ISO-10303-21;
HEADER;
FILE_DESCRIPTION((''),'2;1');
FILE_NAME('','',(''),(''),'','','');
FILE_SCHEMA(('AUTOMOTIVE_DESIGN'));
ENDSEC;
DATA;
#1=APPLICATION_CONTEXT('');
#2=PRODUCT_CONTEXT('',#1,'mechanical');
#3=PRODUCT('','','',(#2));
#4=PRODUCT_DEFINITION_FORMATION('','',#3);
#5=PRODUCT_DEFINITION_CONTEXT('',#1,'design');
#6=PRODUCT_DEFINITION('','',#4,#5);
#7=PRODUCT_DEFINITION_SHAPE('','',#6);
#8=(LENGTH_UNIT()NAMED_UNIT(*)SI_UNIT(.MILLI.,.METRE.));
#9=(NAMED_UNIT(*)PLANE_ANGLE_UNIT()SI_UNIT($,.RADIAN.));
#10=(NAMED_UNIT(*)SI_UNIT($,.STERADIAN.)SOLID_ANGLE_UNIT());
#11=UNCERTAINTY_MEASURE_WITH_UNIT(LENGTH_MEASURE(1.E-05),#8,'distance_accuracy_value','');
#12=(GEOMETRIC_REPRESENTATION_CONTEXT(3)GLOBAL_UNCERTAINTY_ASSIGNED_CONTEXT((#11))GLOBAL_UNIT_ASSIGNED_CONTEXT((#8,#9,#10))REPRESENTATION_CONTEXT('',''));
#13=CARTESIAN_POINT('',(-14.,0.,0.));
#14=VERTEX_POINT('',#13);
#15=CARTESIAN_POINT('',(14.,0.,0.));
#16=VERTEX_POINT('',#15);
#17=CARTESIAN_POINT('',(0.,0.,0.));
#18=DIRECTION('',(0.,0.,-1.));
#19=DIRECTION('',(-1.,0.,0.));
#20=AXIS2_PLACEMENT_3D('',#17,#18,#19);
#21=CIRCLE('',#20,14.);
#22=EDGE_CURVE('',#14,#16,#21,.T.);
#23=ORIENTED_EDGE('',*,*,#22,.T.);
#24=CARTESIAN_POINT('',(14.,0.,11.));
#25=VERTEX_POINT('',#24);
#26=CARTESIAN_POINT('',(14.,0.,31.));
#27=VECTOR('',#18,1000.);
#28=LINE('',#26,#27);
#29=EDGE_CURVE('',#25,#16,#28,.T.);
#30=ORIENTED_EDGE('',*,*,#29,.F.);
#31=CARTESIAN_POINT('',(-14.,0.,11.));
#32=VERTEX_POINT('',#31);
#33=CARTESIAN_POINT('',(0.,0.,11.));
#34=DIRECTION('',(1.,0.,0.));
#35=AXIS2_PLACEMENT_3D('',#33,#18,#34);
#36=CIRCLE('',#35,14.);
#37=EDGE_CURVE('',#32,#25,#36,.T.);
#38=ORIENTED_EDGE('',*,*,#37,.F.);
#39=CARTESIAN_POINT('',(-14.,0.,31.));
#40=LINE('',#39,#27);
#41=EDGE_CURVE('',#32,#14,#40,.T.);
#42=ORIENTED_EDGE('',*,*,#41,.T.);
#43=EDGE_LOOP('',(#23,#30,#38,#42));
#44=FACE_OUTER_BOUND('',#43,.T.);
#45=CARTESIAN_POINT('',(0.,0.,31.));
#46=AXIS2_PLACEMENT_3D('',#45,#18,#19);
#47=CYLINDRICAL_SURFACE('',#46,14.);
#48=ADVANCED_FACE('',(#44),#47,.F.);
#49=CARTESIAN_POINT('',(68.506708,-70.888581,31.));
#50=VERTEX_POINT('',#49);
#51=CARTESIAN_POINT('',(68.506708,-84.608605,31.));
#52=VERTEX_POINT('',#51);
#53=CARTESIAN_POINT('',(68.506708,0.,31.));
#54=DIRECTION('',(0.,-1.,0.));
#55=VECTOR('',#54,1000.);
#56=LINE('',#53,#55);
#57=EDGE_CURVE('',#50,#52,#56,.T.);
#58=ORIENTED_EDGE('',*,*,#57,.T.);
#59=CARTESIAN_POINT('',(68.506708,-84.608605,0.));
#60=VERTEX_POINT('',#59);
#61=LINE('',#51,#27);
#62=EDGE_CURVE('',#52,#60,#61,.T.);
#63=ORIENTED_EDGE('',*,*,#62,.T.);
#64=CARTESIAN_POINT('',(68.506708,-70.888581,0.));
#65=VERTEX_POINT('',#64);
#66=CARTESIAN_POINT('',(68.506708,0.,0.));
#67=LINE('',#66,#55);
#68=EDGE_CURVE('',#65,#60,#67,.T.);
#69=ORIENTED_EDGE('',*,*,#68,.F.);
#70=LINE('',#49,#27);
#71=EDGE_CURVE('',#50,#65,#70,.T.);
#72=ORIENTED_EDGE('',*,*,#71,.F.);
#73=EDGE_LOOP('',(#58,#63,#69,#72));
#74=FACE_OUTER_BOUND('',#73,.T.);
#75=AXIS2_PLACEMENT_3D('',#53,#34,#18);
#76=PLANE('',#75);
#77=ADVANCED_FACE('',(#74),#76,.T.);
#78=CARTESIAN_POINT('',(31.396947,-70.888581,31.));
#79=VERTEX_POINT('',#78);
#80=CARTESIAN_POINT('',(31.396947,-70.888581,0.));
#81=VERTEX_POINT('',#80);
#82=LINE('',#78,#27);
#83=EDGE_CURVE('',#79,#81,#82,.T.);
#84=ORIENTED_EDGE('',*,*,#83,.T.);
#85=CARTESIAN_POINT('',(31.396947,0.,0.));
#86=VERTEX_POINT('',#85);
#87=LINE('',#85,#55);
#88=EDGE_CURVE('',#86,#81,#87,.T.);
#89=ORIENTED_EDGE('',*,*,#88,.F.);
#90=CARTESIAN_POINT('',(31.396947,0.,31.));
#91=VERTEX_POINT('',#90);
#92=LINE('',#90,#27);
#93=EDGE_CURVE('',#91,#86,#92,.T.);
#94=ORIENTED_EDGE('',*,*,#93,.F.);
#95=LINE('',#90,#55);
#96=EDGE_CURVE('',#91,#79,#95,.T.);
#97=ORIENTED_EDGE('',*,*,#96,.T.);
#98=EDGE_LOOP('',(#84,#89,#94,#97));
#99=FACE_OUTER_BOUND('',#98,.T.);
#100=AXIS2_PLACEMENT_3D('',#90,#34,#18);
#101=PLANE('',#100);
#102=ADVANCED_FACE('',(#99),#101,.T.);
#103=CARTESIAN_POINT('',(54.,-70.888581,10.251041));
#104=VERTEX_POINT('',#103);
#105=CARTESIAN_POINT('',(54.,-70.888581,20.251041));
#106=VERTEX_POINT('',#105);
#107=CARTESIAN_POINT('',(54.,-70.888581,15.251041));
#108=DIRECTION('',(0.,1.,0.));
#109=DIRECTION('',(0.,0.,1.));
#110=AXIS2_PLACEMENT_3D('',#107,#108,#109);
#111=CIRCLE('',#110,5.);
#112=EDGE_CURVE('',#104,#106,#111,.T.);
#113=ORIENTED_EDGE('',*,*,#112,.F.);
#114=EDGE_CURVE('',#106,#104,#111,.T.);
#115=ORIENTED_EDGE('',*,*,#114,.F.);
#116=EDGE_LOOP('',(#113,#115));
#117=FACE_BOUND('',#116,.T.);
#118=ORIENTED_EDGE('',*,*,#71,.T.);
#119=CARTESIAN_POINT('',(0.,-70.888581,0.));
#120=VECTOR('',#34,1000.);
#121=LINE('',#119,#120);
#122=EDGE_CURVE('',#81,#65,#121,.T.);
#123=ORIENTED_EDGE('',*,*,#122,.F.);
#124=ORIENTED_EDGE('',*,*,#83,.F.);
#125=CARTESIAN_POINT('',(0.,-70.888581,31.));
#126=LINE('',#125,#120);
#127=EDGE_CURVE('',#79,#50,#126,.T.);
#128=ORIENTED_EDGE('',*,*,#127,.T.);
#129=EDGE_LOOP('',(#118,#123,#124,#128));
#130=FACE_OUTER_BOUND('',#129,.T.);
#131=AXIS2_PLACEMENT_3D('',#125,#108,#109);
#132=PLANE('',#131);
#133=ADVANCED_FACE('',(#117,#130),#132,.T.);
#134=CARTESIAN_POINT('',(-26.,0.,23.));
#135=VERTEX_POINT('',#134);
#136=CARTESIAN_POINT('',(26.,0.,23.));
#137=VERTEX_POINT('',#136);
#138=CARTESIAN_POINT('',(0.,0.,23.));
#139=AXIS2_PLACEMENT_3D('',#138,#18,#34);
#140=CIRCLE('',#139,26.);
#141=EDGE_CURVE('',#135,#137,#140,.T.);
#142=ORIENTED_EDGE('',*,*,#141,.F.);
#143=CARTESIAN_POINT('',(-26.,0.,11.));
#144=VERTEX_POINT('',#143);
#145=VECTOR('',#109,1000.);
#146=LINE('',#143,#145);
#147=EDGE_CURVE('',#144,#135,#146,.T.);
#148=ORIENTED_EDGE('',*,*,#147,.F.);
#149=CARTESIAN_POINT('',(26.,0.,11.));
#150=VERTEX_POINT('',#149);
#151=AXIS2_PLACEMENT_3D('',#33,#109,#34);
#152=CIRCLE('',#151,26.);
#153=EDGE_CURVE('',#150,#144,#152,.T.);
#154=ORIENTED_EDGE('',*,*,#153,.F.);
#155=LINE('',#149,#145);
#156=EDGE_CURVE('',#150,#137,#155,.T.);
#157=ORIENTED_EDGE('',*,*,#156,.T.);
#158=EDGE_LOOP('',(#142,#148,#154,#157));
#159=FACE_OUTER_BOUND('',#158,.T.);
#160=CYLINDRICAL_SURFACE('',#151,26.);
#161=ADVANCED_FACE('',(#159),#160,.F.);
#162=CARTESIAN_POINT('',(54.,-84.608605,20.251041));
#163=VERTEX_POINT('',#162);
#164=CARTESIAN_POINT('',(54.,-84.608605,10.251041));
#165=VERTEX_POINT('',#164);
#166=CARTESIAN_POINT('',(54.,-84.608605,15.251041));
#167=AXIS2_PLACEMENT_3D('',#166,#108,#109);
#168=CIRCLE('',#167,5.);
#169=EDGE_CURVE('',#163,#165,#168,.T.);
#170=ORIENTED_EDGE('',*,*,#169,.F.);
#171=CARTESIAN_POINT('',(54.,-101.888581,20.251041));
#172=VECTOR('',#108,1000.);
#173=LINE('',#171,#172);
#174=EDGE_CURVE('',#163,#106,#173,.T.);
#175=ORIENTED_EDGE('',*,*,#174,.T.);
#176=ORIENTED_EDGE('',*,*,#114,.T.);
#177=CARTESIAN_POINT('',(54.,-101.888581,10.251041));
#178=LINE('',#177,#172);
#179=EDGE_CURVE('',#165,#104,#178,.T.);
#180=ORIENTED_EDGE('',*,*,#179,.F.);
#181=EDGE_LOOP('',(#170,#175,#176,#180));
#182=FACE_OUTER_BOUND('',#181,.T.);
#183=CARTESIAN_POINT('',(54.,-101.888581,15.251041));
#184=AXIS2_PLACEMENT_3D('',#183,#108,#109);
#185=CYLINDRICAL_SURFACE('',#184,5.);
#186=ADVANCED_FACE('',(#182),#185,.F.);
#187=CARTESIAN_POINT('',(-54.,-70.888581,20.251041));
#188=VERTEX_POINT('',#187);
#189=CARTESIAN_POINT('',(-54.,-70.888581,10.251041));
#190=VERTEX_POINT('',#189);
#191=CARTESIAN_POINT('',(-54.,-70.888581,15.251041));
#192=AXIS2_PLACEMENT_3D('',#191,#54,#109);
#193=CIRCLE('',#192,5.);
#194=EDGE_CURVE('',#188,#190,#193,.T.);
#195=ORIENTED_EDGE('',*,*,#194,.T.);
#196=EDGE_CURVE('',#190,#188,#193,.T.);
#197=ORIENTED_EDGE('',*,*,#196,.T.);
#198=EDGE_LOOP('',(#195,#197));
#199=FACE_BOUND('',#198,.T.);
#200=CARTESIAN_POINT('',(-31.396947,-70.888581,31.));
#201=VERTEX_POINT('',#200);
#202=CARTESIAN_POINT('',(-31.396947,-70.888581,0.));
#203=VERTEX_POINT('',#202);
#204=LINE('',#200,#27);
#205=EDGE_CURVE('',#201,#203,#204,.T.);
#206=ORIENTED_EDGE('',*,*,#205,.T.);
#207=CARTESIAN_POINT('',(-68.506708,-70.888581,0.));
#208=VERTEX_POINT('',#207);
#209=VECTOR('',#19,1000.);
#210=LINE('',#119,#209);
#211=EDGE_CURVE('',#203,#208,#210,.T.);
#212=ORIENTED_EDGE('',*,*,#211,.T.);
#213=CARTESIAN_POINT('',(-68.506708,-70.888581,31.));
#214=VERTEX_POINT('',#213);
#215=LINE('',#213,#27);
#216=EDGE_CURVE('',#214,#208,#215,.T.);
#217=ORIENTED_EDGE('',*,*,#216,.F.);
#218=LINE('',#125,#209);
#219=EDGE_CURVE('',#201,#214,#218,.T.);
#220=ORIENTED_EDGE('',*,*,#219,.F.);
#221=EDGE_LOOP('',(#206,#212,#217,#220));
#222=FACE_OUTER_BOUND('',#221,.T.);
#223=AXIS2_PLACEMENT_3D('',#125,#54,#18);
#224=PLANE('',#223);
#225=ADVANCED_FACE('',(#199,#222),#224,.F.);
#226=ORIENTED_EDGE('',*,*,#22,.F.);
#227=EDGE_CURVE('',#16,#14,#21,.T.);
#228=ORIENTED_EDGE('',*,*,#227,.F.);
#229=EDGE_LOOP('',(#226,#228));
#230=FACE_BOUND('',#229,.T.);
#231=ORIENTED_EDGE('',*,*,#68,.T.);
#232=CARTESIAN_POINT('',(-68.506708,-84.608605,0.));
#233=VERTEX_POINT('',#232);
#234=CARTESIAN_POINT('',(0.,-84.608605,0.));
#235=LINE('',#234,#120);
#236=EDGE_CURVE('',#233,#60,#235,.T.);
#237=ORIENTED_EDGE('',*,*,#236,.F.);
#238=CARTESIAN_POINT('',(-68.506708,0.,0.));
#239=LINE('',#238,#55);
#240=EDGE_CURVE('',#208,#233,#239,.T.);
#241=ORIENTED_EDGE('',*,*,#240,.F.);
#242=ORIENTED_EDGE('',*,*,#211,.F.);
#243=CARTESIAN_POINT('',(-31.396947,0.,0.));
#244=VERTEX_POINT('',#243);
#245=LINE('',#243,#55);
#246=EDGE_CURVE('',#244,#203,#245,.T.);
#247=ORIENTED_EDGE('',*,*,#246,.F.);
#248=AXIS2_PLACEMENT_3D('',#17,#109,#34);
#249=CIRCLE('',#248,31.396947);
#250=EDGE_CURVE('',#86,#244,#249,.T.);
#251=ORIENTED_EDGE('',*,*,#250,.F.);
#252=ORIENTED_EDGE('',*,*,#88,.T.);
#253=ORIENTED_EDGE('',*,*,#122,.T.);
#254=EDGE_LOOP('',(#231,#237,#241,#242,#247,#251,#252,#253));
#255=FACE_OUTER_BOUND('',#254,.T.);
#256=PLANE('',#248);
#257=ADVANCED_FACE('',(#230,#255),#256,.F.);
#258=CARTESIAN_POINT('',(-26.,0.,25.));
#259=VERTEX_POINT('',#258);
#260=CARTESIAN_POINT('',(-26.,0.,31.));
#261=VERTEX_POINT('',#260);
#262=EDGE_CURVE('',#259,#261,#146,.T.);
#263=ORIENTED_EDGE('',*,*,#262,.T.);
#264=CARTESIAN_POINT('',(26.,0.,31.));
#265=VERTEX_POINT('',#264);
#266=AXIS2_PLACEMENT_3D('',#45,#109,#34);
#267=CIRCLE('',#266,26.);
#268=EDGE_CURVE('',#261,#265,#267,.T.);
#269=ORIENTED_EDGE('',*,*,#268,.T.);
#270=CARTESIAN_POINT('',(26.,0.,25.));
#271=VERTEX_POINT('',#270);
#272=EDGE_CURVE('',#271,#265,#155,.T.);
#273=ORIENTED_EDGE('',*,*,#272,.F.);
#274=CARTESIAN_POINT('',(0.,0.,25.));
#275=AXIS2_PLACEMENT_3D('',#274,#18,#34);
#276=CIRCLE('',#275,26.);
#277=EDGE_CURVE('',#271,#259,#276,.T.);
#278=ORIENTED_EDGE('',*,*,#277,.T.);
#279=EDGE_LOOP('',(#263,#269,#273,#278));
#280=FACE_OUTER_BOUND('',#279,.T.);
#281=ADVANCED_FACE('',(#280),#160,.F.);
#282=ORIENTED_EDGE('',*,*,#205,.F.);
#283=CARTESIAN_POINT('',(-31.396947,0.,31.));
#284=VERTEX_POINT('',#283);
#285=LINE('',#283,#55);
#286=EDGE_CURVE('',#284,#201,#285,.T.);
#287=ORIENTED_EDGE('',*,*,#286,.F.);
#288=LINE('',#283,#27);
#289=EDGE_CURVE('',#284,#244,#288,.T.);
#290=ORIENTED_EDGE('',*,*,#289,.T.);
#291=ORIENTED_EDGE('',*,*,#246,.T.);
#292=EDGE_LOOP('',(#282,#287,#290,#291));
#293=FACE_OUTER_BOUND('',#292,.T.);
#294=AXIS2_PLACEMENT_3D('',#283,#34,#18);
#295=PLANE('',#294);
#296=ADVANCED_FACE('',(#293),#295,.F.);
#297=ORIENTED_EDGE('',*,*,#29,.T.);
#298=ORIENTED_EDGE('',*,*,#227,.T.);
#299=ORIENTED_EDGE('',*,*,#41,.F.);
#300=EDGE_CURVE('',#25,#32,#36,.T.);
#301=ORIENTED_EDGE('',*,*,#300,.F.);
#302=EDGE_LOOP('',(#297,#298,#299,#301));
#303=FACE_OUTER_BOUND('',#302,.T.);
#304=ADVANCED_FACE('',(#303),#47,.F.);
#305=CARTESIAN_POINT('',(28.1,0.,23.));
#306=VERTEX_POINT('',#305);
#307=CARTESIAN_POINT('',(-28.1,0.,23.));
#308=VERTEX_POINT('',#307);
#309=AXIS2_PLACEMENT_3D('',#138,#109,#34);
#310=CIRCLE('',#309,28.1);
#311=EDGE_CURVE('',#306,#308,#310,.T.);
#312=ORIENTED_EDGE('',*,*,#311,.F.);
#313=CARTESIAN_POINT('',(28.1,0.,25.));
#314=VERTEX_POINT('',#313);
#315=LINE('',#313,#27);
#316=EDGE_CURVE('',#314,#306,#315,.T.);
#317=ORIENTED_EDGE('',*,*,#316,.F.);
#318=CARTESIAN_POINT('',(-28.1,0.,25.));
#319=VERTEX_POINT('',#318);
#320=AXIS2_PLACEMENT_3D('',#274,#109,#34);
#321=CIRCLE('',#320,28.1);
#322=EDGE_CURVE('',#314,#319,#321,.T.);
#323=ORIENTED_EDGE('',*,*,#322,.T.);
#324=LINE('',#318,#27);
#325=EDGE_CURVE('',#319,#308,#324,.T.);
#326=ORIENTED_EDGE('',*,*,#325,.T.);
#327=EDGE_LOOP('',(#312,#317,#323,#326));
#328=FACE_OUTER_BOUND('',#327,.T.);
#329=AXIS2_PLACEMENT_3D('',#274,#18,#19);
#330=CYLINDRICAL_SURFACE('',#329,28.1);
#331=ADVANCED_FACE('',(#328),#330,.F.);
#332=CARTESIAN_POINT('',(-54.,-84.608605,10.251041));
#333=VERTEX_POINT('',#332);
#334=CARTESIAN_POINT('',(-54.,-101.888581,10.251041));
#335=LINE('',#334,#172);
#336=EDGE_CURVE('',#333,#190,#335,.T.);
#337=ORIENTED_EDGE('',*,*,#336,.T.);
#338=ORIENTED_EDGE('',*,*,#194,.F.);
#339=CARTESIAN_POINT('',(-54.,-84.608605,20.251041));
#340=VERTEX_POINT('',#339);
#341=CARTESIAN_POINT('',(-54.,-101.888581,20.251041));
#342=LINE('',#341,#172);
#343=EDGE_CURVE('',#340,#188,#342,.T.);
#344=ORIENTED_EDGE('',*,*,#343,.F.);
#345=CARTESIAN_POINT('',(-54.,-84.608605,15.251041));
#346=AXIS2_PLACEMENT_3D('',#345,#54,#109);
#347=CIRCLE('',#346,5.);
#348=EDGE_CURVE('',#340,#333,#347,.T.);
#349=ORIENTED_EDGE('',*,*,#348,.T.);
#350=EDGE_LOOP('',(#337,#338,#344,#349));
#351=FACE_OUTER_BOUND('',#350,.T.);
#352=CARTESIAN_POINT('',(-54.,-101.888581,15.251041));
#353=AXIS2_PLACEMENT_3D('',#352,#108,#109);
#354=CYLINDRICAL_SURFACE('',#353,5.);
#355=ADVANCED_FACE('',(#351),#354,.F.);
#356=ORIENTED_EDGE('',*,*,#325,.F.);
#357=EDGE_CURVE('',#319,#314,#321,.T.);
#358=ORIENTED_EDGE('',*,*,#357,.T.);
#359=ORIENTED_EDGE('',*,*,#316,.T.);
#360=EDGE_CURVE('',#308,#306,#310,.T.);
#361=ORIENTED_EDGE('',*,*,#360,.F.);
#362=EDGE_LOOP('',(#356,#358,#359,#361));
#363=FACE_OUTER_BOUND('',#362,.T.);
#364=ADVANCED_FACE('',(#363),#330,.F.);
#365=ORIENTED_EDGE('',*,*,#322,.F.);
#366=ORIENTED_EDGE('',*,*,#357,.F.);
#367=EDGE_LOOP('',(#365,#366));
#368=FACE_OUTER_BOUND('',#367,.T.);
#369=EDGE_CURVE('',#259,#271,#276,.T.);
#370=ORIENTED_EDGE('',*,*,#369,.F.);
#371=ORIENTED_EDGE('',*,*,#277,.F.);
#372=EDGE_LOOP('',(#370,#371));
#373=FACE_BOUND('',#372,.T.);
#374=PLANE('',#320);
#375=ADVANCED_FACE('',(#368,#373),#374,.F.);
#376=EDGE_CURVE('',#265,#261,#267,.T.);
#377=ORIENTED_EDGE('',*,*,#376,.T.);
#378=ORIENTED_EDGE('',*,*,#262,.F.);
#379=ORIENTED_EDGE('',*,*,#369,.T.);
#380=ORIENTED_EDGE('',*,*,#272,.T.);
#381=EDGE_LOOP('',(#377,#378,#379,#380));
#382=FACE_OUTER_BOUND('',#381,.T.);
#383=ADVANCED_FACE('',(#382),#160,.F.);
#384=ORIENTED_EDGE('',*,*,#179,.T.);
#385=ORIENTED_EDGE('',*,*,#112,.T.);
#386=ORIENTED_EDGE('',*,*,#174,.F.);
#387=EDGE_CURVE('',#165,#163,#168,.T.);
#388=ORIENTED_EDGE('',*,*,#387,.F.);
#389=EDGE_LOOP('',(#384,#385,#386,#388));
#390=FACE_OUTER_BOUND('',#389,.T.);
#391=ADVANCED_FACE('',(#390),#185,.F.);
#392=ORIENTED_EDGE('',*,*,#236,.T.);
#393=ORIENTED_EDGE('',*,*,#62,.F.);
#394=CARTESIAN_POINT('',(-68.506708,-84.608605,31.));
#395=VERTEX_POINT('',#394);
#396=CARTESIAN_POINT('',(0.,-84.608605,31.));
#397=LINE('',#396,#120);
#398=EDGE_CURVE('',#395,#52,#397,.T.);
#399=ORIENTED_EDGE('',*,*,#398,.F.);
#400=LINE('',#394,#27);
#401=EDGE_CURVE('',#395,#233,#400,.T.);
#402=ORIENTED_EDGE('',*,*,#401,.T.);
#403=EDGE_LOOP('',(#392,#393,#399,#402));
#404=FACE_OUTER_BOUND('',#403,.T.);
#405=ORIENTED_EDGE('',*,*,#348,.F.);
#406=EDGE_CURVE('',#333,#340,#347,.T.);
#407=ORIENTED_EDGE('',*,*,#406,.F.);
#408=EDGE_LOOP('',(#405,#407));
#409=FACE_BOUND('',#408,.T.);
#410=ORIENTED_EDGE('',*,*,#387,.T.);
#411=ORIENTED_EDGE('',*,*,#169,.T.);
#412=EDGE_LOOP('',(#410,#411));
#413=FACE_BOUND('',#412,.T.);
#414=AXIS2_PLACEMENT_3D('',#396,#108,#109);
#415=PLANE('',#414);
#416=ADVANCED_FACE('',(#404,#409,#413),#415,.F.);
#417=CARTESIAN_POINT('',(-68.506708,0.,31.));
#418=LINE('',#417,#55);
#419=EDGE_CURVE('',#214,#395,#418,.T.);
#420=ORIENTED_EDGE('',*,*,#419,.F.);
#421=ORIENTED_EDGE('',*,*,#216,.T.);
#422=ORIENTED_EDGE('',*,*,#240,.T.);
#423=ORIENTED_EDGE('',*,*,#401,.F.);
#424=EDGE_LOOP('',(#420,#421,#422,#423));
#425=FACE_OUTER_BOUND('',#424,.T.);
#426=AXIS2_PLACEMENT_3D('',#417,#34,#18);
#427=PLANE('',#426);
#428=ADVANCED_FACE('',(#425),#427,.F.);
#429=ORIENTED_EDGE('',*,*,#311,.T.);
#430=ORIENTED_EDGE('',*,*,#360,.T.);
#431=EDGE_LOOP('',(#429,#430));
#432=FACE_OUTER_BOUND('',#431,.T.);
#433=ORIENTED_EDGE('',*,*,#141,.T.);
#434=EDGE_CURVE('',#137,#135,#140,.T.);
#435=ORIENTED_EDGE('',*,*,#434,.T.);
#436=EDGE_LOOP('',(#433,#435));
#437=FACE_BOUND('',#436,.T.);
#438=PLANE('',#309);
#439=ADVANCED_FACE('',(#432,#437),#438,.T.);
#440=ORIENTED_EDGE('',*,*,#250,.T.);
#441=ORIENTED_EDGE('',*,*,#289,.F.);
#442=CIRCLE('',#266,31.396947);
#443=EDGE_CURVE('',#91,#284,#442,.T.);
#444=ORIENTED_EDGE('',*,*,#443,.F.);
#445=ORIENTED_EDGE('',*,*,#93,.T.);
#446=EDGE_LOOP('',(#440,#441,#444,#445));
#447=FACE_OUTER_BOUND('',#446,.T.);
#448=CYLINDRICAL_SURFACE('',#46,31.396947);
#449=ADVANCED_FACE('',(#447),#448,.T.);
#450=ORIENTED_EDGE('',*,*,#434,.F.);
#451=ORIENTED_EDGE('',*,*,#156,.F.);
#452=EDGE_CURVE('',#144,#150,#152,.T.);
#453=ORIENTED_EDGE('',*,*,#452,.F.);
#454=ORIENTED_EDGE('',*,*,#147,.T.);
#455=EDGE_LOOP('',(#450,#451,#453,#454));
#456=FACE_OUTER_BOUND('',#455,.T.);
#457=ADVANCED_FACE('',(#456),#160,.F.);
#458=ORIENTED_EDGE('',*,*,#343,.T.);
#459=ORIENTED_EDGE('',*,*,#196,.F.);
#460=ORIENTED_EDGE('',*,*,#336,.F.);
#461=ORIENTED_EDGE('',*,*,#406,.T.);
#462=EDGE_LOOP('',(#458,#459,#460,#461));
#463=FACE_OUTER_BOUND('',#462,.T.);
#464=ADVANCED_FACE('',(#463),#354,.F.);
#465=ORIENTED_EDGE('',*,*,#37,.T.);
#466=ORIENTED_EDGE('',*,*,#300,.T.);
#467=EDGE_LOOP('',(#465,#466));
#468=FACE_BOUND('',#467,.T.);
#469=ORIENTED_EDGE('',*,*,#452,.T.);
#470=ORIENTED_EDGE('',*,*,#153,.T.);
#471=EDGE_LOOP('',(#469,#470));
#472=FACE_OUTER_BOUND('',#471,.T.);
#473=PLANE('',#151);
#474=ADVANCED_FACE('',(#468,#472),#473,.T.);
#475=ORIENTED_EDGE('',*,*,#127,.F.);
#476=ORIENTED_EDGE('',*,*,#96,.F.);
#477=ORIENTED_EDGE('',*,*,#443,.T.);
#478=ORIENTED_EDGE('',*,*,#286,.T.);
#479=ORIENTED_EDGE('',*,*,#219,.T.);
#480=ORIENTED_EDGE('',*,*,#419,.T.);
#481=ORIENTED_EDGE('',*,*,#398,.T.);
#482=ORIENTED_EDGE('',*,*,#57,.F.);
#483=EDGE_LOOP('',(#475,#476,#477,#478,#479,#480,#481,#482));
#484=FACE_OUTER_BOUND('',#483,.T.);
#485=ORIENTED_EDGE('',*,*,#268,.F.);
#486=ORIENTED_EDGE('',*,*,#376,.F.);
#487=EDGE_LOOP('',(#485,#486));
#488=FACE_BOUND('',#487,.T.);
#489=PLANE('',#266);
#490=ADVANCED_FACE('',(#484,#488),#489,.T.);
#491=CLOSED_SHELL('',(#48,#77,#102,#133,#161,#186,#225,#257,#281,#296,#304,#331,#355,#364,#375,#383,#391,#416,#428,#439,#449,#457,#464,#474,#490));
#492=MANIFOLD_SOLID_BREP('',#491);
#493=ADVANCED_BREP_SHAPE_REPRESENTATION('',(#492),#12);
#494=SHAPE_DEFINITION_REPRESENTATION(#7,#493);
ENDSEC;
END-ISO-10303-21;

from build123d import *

# Parameters (mm, degrees)
SKETCH1_R           = 31.396947085
SKETCH1_R_2         = 12.5
BOSS_EXTRUDE1_DEPTH = 31
SKETCH2_R           = 5
CUT_EXTRUDE1_DEPTH  = 31
SKETCH3_R           = 14
CUT_EXTRUDE2_DEPTH  = 114.19357359
SKETCH5_R           = 26
CUT_EXTRUDE4_DEPTH  = 20
SKETCH6_R           = 28.1
CUT_EXTRUDE5_DEPTH  = 2


with BuildPart() as part:
    # Sketch1 → Boss-Extrude1 (new body)
    # profile 1 of 2: a face of its own
    with BuildSketch(Plane.XY):
        Circle(SKETCH1_R)
        with Locations(Location((0, 0, 0), (0, 0, 180))):
            Circle(SKETCH1_R_2, mode=Mode.SUBTRACT)
    # profile 2 of 2: a face of its own
    with BuildSketch(Plane.XY):
        with BuildLine():
            ThreePointArc((31.396947085, 0), (0, -31.396947085), (-31.396947085, 0))
            Line((-31.396947085, 0), (-31.396947085, -70.888581066))
            Line((-31.396947085, -70.888581066), (-68.506708087, -70.888581066))
            Line((-68.506708087, -70.888581066), (-68.506708087, -84.608605054))
            Line((-68.506708087, -84.608605054), (68.506708087, -84.608605054))
            Line((68.506708087, -84.608605054), (68.506708087, -70.888581066))
            Line((68.506708087, -70.888581066), (31.396947085, -70.888581066))
            Line((31.396947085, -70.888581066), (31.396947085, 0))
        make_face()
    extrude(amount=BOSS_EXTRUDE1_DEPTH)

    # Sketch2 → Cut-Extrude1 (cut)
    with BuildSketch(Plane(origin=(0, -70.888581066, 0), x_dir=(1, 0, 0), z_dir=(0, 1, 0))):
        with Locations(Location((54, -15.251041139, 0), (0, 0, 270))):
            Circle(SKETCH2_R)
        with Locations(Location((-54, -15.251041139, 0), (0, 0, 270))):
            Circle(SKETCH2_R)
    extrude(amount=-CUT_EXTRUDE1_DEPTH, mode=Mode.SUBTRACT)

    # Sketch3 → Cut-Extrude2 (cut, through all)
    with BuildSketch(Plane(origin=(0, 0, 0), x_dir=(-1, 0, 0), z_dir=(0, 0, -1))):
        Circle(SKETCH3_R)
    extrude(amount=-CUT_EXTRUDE2_DEPTH, mode=Mode.SUBTRACT)

    # Sketch5 → Cut-Extrude4 (cut)
    with BuildSketch(Plane.XY.offset(31)):
        Circle(SKETCH5_R)
    extrude(amount=-CUT_EXTRUDE4_DEPTH, mode=Mode.SUBTRACT)

    # Sketch6 → Cut-Extrude5 (cut)
    with BuildSketch(Plane.XY.offset(23)):
        Circle(SKETCH6_R)
    extrude(amount=CUT_EXTRUDE5_DEPTH, mode=Mode.SUBTRACT)


solid = part.part
